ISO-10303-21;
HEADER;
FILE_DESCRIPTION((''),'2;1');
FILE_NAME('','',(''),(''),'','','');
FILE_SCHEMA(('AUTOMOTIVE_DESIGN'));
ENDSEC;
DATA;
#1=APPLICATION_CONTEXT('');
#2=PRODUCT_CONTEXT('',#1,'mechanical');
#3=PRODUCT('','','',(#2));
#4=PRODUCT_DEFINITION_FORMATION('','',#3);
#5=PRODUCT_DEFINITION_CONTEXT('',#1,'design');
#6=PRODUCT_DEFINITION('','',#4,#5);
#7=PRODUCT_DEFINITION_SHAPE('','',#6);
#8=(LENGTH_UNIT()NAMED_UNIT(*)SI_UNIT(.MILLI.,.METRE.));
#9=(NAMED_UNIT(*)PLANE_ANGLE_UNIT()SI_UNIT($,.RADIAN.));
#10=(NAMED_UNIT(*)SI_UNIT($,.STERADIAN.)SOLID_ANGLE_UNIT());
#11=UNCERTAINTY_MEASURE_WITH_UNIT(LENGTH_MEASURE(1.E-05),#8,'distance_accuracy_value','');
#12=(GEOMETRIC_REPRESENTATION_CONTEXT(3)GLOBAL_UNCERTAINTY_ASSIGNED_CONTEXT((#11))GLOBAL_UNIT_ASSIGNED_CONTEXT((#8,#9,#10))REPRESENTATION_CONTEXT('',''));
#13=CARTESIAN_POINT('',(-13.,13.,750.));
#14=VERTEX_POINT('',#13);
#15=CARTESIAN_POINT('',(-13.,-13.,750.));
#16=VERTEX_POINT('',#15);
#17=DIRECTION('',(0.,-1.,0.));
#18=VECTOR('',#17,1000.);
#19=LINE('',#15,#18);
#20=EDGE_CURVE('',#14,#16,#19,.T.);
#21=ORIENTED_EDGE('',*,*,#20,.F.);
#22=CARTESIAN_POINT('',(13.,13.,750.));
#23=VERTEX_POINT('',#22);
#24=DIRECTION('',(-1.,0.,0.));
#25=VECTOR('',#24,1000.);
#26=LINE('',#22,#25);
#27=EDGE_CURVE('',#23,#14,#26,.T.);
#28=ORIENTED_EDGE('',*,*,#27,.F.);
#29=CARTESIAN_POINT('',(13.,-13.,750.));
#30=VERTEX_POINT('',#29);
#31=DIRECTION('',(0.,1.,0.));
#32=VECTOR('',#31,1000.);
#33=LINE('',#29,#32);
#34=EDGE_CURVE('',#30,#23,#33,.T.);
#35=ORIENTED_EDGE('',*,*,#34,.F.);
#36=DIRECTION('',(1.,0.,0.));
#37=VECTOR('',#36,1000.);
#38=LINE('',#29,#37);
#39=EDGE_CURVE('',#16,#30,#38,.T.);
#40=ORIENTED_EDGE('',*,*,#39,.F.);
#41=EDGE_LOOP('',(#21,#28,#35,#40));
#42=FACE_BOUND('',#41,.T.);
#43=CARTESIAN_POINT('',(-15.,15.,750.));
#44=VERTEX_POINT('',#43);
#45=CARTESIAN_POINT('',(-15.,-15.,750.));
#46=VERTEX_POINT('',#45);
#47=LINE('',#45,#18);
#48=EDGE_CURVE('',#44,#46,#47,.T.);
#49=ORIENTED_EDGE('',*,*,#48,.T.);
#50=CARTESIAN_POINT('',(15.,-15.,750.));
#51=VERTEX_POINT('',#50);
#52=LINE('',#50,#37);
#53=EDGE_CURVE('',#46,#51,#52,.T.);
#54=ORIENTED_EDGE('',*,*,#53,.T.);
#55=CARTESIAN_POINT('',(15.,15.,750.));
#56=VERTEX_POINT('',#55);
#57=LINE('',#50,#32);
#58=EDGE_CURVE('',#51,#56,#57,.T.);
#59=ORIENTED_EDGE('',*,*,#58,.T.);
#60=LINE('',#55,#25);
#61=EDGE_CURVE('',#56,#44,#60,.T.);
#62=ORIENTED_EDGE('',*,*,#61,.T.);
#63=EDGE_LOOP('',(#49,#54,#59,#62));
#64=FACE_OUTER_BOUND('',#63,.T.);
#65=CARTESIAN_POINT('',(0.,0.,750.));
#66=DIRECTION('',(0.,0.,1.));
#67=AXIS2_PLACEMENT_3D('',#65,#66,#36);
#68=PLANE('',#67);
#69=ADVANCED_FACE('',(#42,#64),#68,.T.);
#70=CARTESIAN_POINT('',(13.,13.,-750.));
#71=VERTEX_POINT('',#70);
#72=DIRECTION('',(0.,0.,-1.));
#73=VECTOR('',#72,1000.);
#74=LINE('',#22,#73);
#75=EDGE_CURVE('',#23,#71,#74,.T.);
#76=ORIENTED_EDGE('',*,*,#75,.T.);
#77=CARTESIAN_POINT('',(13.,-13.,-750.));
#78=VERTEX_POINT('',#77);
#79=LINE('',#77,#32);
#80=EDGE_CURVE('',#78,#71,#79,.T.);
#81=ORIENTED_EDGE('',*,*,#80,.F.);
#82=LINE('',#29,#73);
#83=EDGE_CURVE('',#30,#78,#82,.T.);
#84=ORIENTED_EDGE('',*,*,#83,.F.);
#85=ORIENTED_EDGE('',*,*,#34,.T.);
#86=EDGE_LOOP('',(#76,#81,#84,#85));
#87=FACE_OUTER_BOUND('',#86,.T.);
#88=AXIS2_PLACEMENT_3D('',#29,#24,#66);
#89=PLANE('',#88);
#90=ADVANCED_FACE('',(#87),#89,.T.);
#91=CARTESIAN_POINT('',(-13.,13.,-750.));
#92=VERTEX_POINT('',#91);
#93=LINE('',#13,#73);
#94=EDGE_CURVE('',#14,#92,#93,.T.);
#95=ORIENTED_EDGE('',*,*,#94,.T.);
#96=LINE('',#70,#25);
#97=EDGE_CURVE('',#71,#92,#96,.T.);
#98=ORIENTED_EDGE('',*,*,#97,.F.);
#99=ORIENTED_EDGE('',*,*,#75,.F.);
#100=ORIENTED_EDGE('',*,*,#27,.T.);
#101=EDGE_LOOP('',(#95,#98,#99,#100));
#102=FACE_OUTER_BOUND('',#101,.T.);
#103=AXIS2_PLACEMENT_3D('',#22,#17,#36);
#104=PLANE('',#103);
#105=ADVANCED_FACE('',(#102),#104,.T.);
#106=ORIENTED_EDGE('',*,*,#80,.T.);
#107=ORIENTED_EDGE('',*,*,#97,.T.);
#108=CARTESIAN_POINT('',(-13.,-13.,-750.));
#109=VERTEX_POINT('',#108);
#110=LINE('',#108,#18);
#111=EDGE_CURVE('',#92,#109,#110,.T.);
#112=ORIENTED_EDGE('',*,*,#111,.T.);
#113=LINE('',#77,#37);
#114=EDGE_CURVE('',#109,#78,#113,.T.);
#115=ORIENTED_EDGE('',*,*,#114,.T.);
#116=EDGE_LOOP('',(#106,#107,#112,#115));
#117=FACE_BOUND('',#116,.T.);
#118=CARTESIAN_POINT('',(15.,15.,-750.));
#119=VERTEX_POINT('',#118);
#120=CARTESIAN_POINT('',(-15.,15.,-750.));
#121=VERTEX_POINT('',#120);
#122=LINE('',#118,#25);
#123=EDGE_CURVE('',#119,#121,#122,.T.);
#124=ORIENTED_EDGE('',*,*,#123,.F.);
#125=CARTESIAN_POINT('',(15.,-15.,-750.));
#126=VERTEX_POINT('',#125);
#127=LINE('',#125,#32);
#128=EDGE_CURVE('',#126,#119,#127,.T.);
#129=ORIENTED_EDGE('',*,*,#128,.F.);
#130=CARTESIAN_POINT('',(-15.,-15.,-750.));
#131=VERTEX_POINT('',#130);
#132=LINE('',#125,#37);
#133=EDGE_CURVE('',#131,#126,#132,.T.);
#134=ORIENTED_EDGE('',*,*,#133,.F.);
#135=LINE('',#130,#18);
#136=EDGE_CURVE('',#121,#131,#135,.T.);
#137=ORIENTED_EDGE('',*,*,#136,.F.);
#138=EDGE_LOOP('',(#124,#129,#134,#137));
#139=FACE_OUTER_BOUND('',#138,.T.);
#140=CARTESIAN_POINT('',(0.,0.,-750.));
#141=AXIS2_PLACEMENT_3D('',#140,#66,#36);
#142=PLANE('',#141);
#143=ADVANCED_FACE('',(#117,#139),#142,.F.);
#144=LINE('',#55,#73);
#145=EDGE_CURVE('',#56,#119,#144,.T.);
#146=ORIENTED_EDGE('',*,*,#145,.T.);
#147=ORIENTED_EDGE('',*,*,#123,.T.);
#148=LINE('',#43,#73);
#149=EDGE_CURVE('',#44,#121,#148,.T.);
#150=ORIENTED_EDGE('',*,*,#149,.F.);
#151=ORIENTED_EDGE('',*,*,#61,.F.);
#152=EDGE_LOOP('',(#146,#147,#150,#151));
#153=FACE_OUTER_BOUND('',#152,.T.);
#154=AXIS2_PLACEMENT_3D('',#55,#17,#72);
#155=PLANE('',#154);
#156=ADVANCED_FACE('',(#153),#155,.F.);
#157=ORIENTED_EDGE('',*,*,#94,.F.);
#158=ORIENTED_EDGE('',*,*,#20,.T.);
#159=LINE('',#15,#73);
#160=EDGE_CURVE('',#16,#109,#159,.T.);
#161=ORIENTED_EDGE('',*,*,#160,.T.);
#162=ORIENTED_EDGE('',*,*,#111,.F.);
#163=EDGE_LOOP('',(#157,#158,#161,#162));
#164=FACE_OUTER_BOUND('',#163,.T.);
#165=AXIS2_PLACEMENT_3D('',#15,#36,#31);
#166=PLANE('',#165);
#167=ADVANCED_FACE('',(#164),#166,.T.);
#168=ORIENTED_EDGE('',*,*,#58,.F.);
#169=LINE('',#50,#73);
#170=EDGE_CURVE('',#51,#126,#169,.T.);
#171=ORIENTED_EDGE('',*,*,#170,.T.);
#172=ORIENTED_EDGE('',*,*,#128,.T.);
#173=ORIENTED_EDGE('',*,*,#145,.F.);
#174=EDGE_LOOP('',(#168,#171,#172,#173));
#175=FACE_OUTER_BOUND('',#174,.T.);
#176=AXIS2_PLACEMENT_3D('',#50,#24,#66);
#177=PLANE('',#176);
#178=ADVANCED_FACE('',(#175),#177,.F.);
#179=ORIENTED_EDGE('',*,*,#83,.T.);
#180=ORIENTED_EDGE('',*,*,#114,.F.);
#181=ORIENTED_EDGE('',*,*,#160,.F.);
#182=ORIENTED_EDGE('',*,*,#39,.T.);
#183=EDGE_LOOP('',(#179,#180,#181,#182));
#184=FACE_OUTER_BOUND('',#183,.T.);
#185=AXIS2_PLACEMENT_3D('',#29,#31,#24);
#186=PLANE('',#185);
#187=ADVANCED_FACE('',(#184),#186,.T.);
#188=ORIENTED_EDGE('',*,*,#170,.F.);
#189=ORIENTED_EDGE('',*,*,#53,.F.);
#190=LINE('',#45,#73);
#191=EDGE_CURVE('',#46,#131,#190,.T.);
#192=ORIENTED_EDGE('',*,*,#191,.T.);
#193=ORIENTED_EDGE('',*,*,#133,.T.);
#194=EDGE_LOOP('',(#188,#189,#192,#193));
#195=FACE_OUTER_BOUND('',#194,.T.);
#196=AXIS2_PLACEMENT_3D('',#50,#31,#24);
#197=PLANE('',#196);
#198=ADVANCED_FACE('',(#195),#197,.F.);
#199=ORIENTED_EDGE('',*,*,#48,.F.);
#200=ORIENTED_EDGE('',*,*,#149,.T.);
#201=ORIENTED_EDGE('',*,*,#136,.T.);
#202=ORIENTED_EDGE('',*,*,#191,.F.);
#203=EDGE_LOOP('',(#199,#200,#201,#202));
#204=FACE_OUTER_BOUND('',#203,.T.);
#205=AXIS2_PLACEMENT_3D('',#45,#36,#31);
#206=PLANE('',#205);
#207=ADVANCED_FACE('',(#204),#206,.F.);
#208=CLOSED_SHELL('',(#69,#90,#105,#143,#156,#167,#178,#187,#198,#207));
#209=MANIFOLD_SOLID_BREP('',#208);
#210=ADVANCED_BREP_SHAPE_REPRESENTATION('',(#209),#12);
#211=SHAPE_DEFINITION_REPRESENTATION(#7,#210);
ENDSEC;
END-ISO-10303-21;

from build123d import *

# Parameters (mm, degrees)
SKETCH_1_W      = 30
SKETCH_1_H      = 30
SKETCH_1_W_2    = 26
SKETCH_1_H_2    = 26
EXTRUDE_1_DEPTH = 750


with BuildPart() as part:
    # 草图1 → 凸台-拉伸1 (new, symmetric)
    with BuildSketch(Plane.XY):
        Rectangle(SKETCH_1_W, SKETCH_1_H)
        Rectangle(SKETCH_1_W_2, SKETCH_1_H_2, mode=Mode.SUBTRACT)
    extrude(amount=EXTRUDE_1_DEPTH, both=True)


solid = part.part
